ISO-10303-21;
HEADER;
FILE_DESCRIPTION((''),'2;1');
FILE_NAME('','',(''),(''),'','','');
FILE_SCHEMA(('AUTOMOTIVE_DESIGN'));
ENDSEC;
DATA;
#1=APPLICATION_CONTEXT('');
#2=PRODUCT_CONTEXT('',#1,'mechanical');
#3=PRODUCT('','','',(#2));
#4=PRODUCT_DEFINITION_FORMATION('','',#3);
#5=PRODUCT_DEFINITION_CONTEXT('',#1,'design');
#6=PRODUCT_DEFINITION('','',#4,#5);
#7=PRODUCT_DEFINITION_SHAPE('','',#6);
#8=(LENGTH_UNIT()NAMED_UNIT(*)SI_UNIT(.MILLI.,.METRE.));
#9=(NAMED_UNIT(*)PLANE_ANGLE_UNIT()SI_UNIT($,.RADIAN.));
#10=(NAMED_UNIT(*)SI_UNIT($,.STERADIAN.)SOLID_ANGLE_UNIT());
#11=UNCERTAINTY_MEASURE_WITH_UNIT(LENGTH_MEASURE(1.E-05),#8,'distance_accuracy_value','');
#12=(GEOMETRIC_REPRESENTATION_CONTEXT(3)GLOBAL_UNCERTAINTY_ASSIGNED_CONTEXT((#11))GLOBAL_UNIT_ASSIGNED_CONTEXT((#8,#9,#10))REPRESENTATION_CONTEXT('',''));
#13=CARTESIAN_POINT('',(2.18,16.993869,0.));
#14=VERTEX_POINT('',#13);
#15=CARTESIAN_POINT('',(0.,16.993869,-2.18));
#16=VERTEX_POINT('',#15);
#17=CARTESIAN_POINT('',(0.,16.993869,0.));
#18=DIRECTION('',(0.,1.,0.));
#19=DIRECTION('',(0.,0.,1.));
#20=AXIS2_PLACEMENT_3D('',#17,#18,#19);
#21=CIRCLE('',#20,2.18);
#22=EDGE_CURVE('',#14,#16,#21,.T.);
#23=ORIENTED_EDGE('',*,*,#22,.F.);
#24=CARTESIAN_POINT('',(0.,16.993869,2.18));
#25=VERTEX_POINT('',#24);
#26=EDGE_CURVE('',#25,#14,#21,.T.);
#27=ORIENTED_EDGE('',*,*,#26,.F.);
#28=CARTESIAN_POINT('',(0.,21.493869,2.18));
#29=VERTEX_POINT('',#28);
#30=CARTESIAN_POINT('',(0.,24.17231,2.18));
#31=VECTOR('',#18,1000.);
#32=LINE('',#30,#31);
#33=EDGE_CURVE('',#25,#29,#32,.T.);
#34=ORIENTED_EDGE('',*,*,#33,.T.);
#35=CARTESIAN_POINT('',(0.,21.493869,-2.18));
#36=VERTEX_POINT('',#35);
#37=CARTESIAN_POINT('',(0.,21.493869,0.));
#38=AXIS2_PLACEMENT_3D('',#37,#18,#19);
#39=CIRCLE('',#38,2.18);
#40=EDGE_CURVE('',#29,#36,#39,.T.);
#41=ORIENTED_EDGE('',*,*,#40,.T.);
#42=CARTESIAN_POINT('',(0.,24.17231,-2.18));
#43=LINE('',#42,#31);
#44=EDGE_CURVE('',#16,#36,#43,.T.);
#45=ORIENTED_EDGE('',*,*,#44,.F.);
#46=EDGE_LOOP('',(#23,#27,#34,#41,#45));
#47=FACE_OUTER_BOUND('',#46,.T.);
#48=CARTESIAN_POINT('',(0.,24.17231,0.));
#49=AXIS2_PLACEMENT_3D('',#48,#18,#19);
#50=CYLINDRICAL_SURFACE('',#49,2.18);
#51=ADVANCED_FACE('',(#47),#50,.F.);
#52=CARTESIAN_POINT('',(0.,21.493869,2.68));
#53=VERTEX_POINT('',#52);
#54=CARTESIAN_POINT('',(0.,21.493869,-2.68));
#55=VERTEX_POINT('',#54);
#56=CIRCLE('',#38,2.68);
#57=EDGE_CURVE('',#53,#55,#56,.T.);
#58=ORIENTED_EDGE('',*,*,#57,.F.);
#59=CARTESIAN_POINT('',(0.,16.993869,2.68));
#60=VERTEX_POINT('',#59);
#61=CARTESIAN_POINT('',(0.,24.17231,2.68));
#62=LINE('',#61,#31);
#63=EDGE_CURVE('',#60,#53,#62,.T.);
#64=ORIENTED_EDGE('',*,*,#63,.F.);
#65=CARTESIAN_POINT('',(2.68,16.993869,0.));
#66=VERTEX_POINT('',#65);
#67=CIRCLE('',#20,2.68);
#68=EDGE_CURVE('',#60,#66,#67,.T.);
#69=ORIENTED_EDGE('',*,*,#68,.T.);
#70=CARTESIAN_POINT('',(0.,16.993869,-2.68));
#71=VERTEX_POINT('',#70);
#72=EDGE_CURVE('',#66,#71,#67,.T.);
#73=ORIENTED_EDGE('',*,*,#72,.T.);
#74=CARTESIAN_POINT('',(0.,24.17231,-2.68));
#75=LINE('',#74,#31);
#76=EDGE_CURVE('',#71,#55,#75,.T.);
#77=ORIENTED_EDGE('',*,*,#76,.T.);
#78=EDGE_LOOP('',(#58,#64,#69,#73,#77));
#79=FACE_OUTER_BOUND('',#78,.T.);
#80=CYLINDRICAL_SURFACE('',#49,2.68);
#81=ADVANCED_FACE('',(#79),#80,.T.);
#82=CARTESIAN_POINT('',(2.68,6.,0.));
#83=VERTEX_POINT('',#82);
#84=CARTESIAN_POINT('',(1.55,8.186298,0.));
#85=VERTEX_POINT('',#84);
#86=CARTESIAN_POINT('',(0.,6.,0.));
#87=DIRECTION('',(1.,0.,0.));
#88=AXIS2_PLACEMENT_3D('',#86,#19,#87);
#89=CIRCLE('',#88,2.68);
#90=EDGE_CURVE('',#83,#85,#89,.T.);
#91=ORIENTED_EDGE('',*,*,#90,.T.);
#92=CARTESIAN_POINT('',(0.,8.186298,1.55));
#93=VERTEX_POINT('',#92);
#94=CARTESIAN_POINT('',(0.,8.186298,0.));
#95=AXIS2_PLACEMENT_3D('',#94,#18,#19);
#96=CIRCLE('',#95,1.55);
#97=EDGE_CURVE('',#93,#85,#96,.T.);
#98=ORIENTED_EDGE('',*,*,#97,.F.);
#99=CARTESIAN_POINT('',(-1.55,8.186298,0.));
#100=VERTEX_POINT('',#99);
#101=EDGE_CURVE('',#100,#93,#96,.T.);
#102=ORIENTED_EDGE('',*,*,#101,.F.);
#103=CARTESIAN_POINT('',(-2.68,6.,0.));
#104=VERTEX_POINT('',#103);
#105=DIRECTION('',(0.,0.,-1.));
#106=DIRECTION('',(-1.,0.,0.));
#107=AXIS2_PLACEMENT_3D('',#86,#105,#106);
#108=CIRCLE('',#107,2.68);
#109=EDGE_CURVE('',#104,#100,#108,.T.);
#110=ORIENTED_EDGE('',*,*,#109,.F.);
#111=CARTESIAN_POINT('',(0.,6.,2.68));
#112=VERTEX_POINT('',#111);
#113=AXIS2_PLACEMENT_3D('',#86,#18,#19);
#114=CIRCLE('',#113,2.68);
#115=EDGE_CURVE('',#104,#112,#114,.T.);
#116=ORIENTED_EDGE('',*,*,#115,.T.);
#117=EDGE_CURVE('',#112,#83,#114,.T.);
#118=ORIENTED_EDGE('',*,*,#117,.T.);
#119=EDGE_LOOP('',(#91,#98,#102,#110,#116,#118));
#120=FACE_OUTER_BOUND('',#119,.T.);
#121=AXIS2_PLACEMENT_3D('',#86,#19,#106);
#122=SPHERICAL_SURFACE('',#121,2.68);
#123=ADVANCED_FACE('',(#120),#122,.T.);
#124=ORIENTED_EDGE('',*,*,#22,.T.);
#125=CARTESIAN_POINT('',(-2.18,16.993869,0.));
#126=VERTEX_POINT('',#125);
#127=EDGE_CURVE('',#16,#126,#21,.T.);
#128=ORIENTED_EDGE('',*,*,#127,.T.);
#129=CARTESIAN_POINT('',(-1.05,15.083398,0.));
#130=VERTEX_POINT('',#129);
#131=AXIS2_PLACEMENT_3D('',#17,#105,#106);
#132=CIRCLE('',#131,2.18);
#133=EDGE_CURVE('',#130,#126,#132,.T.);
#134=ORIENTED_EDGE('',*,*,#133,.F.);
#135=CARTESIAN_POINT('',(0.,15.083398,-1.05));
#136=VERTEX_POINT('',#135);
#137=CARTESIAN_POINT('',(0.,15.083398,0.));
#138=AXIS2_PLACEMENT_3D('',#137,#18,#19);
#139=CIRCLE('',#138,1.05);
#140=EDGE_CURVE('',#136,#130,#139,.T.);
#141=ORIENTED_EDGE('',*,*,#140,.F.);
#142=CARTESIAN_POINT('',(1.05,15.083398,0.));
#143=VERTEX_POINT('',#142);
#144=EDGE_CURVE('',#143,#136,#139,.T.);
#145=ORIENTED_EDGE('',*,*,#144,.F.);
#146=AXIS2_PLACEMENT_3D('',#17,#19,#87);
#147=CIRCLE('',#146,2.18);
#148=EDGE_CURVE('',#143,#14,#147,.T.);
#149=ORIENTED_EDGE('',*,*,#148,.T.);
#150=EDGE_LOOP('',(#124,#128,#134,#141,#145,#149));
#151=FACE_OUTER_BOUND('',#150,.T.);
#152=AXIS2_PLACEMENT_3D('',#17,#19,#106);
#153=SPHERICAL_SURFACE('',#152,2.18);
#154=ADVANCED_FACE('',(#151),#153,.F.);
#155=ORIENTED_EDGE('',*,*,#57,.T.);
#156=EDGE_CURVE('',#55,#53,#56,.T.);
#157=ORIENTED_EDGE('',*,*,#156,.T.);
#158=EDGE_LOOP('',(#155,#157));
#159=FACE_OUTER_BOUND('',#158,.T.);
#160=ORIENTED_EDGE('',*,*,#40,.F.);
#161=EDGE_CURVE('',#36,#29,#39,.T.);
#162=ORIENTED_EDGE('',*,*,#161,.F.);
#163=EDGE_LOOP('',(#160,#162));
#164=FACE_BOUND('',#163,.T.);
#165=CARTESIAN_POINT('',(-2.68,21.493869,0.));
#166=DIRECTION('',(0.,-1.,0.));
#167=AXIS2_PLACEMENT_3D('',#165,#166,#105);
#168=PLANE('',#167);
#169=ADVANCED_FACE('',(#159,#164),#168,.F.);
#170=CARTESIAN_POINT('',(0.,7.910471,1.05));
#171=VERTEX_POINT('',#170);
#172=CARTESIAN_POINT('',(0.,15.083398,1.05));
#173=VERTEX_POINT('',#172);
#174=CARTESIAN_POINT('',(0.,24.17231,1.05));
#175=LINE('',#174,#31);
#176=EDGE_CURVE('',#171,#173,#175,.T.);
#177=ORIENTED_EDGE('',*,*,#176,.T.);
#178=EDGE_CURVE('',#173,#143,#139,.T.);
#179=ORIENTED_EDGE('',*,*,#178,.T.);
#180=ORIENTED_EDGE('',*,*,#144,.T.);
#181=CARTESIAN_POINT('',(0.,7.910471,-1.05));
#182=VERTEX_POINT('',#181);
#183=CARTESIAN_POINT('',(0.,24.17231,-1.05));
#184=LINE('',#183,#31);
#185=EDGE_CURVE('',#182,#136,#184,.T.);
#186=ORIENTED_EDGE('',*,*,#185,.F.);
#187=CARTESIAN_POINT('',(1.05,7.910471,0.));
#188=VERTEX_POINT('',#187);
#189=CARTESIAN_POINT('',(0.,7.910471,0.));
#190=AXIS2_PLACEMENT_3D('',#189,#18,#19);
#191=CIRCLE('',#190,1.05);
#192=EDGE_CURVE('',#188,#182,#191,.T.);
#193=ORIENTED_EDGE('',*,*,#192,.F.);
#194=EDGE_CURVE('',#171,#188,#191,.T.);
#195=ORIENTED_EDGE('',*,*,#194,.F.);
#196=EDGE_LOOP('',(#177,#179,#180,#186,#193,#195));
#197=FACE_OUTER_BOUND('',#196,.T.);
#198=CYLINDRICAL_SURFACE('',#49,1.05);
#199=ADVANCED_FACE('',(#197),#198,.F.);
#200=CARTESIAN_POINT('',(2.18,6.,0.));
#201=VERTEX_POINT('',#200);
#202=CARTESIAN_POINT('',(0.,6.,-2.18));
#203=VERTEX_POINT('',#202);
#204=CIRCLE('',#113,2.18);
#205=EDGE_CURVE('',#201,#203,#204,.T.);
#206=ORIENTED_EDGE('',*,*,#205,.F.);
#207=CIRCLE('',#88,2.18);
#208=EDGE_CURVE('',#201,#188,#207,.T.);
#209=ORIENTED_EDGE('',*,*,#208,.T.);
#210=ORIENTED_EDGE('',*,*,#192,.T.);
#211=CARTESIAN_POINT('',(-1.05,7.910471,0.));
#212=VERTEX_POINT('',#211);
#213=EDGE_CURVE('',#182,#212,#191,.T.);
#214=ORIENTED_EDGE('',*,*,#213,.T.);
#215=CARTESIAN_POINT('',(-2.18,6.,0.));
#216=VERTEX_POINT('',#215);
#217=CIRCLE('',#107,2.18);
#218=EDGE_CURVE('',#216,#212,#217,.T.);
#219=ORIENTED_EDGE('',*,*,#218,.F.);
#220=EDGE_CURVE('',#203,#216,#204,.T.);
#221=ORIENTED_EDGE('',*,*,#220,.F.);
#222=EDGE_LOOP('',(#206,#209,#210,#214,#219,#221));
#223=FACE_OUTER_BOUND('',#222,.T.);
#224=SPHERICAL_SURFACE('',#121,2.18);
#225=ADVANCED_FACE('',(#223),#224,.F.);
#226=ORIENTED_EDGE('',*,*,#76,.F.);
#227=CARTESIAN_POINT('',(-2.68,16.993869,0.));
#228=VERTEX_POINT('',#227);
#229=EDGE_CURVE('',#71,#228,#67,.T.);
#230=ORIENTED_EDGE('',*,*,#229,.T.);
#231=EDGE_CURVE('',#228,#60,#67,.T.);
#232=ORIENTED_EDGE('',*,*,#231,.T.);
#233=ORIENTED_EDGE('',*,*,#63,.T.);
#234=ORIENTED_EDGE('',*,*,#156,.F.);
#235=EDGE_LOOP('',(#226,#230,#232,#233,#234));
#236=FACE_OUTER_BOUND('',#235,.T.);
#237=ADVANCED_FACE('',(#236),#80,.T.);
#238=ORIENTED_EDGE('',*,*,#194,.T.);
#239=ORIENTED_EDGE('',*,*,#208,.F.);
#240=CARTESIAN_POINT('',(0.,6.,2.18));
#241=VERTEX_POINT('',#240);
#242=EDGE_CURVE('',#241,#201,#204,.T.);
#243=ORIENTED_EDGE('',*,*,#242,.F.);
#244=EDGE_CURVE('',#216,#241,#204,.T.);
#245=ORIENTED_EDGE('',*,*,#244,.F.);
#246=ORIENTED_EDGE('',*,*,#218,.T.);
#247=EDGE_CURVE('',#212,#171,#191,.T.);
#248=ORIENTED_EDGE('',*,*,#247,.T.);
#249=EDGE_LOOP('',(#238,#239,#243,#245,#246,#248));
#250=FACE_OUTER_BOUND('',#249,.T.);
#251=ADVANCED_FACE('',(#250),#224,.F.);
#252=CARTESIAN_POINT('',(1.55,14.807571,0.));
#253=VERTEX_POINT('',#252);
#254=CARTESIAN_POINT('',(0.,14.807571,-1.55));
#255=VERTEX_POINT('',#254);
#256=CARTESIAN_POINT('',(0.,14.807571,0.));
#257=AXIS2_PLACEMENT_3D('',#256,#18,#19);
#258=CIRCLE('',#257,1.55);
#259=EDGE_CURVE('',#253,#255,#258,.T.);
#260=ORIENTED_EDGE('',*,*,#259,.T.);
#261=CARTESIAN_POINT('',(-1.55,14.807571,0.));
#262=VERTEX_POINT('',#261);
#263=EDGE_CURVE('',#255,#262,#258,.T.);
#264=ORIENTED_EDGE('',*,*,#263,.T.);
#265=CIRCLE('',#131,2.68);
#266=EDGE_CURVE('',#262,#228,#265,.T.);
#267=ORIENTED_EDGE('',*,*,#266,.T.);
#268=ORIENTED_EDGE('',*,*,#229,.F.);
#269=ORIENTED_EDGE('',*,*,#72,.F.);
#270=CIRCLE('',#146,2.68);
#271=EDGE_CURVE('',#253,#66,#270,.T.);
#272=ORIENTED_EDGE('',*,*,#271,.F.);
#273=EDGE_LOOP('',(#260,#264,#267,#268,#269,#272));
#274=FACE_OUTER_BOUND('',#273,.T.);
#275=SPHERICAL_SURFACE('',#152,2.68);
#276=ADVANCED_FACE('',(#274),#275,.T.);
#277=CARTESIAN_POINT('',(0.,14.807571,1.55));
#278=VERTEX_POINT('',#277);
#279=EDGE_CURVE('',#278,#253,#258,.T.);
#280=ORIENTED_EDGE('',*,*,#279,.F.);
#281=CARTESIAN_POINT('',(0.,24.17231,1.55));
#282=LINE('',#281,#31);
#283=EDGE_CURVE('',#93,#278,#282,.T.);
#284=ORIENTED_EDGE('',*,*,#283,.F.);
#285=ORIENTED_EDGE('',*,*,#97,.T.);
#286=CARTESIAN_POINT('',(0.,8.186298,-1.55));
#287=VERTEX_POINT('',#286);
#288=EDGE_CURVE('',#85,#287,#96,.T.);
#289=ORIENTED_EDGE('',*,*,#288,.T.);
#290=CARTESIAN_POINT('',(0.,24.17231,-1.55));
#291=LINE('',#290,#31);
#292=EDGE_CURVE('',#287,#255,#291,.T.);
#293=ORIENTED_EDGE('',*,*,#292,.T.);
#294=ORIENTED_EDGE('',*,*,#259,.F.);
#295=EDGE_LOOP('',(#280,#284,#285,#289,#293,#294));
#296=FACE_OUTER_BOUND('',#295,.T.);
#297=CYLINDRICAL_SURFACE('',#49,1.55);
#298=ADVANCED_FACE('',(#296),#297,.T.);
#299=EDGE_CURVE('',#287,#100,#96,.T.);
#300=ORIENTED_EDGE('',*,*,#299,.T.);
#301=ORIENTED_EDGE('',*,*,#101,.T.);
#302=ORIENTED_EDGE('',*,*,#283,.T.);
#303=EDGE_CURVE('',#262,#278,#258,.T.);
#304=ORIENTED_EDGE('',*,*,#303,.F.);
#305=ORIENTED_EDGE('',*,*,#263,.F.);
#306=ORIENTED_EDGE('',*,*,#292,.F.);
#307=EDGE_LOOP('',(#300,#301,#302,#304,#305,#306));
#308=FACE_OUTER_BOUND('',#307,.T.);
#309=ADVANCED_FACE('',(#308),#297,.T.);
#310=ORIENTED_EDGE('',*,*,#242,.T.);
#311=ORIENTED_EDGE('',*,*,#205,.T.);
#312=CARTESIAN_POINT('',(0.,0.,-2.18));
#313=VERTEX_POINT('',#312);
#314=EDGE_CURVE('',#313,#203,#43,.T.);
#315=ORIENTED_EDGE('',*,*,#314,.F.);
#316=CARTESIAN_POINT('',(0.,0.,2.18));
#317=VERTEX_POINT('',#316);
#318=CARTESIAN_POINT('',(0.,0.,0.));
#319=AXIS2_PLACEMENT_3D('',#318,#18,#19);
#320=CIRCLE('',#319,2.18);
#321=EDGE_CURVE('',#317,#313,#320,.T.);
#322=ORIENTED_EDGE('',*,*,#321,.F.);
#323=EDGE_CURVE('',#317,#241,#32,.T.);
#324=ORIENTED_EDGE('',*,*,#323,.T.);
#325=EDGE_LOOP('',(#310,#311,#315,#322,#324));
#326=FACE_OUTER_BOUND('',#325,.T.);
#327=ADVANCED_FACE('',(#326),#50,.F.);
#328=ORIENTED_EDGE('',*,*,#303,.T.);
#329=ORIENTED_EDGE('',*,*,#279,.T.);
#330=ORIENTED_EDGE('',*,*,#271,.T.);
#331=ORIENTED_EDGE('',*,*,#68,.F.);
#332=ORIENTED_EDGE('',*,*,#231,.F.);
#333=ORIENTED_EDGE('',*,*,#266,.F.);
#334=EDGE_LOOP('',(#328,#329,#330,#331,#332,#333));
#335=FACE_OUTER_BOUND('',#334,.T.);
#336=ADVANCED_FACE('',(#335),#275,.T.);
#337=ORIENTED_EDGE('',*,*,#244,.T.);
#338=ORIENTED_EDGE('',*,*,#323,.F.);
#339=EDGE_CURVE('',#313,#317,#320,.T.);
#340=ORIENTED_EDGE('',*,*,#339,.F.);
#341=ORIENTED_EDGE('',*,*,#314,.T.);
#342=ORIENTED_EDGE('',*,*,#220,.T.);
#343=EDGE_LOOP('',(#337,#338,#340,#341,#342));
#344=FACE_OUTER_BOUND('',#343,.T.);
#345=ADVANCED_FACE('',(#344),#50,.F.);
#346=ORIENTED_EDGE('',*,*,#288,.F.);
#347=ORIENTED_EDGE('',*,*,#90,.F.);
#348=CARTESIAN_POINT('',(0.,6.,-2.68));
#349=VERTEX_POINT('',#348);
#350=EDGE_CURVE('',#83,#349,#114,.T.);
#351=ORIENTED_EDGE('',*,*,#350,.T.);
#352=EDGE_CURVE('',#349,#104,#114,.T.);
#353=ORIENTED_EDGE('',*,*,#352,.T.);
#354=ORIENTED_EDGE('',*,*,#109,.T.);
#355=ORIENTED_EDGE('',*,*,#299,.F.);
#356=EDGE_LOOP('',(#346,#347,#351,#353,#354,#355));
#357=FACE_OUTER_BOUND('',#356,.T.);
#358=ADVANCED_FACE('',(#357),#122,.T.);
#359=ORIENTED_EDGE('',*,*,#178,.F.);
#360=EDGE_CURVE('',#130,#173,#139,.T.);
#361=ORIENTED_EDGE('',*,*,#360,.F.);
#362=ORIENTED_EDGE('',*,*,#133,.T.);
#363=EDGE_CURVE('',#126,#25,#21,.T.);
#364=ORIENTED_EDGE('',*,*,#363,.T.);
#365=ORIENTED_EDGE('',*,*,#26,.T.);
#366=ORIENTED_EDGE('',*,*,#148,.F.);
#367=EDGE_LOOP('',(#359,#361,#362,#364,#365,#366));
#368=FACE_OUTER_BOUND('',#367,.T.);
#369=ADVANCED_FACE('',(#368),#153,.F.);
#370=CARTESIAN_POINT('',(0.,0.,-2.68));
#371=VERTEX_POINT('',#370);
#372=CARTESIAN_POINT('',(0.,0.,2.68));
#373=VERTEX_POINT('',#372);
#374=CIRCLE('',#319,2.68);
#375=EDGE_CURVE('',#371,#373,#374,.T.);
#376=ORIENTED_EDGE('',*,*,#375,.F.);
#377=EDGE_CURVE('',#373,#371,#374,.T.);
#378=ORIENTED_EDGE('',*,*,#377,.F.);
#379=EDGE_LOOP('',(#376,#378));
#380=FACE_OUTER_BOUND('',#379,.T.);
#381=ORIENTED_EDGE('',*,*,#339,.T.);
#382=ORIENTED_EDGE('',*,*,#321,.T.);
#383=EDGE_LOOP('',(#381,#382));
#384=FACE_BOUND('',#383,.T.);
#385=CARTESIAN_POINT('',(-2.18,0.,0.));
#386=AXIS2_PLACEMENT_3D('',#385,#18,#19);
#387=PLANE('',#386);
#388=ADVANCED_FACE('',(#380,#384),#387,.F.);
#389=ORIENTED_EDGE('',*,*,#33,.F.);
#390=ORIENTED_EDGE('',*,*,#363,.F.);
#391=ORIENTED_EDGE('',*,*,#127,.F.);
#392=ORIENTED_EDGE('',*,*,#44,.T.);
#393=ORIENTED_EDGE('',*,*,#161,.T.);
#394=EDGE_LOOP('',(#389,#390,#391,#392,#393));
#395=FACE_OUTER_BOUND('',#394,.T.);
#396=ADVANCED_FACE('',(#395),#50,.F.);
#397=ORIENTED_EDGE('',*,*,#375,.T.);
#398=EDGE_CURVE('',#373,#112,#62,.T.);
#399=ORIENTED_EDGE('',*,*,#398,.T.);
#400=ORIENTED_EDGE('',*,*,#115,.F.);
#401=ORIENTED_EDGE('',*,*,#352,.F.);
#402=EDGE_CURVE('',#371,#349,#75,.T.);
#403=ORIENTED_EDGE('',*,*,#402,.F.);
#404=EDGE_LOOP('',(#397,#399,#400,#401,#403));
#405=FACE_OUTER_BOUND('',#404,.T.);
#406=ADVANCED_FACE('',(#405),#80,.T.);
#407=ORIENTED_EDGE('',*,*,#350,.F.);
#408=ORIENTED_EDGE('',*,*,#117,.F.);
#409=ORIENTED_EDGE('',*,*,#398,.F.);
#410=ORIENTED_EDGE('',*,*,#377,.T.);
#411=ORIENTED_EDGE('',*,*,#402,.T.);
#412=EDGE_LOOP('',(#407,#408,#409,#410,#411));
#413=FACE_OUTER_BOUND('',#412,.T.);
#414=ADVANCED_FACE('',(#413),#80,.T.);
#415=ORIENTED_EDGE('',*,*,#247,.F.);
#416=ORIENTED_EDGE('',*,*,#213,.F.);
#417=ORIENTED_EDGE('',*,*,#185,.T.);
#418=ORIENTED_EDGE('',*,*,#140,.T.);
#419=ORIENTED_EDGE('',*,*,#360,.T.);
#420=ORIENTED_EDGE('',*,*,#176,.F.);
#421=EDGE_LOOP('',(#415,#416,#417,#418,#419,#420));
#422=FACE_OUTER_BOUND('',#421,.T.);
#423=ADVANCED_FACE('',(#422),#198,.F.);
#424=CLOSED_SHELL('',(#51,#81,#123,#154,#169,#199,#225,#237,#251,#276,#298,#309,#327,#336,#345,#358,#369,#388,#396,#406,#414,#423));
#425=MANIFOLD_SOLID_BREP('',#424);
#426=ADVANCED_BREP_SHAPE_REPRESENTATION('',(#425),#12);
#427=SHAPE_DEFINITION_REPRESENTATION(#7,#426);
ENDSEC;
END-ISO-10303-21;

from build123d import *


with BuildPart() as part:
    # Sketch1 → Revolve-Thin1 (revolve)
    with BuildSketch(Plane.XY, mode=Mode.PRIVATE) as revolve_thin1_sk:
        with BuildLine():
            Line((-2.18, 21.493868799), (-2.18, 16.993868799))
            ThreePointArc((-2.18, 16.993868799), (-1.876352845, 15.884048994), (-1.05, 15.083397653))
            Line((-1.05, 15.083397653), (-1.05, 7.910471146))
            ThreePointArc((-1.05, 7.910471146), (-1.876352845, 7.109819805), (-2.18, 6))
            Line((-2.18, 6), (-2.18, 0))
            Line((-2.18, 0), (-2.68, 0))
            Line((-2.68, 0), (-2.68, 6))
            ThreePointArc((-2.68, 6), (-2.380798185, 7.230528342), (-1.55, 8.186298241))
            Line((-1.55, 8.186298241), (-1.55, 14.807570558))
            ThreePointArc((-1.55, 14.807570558), (-2.380798185, 15.763340457), (-2.68, 16.993868799))
            Line((-2.68, 16.993868799), (-2.68, 21.493868799))
            Line((-2.68, 21.493868799), (-2.18, 21.493868799))
        make_face()
    revolve(revolve_thin1_sk.sketch.rotate(Axis((0, 24.17230999, 0), (0, -1, 0)), 270), axis=Axis((0, 24.17230999, 0), (0, -1, 0)))


solid = part.part
